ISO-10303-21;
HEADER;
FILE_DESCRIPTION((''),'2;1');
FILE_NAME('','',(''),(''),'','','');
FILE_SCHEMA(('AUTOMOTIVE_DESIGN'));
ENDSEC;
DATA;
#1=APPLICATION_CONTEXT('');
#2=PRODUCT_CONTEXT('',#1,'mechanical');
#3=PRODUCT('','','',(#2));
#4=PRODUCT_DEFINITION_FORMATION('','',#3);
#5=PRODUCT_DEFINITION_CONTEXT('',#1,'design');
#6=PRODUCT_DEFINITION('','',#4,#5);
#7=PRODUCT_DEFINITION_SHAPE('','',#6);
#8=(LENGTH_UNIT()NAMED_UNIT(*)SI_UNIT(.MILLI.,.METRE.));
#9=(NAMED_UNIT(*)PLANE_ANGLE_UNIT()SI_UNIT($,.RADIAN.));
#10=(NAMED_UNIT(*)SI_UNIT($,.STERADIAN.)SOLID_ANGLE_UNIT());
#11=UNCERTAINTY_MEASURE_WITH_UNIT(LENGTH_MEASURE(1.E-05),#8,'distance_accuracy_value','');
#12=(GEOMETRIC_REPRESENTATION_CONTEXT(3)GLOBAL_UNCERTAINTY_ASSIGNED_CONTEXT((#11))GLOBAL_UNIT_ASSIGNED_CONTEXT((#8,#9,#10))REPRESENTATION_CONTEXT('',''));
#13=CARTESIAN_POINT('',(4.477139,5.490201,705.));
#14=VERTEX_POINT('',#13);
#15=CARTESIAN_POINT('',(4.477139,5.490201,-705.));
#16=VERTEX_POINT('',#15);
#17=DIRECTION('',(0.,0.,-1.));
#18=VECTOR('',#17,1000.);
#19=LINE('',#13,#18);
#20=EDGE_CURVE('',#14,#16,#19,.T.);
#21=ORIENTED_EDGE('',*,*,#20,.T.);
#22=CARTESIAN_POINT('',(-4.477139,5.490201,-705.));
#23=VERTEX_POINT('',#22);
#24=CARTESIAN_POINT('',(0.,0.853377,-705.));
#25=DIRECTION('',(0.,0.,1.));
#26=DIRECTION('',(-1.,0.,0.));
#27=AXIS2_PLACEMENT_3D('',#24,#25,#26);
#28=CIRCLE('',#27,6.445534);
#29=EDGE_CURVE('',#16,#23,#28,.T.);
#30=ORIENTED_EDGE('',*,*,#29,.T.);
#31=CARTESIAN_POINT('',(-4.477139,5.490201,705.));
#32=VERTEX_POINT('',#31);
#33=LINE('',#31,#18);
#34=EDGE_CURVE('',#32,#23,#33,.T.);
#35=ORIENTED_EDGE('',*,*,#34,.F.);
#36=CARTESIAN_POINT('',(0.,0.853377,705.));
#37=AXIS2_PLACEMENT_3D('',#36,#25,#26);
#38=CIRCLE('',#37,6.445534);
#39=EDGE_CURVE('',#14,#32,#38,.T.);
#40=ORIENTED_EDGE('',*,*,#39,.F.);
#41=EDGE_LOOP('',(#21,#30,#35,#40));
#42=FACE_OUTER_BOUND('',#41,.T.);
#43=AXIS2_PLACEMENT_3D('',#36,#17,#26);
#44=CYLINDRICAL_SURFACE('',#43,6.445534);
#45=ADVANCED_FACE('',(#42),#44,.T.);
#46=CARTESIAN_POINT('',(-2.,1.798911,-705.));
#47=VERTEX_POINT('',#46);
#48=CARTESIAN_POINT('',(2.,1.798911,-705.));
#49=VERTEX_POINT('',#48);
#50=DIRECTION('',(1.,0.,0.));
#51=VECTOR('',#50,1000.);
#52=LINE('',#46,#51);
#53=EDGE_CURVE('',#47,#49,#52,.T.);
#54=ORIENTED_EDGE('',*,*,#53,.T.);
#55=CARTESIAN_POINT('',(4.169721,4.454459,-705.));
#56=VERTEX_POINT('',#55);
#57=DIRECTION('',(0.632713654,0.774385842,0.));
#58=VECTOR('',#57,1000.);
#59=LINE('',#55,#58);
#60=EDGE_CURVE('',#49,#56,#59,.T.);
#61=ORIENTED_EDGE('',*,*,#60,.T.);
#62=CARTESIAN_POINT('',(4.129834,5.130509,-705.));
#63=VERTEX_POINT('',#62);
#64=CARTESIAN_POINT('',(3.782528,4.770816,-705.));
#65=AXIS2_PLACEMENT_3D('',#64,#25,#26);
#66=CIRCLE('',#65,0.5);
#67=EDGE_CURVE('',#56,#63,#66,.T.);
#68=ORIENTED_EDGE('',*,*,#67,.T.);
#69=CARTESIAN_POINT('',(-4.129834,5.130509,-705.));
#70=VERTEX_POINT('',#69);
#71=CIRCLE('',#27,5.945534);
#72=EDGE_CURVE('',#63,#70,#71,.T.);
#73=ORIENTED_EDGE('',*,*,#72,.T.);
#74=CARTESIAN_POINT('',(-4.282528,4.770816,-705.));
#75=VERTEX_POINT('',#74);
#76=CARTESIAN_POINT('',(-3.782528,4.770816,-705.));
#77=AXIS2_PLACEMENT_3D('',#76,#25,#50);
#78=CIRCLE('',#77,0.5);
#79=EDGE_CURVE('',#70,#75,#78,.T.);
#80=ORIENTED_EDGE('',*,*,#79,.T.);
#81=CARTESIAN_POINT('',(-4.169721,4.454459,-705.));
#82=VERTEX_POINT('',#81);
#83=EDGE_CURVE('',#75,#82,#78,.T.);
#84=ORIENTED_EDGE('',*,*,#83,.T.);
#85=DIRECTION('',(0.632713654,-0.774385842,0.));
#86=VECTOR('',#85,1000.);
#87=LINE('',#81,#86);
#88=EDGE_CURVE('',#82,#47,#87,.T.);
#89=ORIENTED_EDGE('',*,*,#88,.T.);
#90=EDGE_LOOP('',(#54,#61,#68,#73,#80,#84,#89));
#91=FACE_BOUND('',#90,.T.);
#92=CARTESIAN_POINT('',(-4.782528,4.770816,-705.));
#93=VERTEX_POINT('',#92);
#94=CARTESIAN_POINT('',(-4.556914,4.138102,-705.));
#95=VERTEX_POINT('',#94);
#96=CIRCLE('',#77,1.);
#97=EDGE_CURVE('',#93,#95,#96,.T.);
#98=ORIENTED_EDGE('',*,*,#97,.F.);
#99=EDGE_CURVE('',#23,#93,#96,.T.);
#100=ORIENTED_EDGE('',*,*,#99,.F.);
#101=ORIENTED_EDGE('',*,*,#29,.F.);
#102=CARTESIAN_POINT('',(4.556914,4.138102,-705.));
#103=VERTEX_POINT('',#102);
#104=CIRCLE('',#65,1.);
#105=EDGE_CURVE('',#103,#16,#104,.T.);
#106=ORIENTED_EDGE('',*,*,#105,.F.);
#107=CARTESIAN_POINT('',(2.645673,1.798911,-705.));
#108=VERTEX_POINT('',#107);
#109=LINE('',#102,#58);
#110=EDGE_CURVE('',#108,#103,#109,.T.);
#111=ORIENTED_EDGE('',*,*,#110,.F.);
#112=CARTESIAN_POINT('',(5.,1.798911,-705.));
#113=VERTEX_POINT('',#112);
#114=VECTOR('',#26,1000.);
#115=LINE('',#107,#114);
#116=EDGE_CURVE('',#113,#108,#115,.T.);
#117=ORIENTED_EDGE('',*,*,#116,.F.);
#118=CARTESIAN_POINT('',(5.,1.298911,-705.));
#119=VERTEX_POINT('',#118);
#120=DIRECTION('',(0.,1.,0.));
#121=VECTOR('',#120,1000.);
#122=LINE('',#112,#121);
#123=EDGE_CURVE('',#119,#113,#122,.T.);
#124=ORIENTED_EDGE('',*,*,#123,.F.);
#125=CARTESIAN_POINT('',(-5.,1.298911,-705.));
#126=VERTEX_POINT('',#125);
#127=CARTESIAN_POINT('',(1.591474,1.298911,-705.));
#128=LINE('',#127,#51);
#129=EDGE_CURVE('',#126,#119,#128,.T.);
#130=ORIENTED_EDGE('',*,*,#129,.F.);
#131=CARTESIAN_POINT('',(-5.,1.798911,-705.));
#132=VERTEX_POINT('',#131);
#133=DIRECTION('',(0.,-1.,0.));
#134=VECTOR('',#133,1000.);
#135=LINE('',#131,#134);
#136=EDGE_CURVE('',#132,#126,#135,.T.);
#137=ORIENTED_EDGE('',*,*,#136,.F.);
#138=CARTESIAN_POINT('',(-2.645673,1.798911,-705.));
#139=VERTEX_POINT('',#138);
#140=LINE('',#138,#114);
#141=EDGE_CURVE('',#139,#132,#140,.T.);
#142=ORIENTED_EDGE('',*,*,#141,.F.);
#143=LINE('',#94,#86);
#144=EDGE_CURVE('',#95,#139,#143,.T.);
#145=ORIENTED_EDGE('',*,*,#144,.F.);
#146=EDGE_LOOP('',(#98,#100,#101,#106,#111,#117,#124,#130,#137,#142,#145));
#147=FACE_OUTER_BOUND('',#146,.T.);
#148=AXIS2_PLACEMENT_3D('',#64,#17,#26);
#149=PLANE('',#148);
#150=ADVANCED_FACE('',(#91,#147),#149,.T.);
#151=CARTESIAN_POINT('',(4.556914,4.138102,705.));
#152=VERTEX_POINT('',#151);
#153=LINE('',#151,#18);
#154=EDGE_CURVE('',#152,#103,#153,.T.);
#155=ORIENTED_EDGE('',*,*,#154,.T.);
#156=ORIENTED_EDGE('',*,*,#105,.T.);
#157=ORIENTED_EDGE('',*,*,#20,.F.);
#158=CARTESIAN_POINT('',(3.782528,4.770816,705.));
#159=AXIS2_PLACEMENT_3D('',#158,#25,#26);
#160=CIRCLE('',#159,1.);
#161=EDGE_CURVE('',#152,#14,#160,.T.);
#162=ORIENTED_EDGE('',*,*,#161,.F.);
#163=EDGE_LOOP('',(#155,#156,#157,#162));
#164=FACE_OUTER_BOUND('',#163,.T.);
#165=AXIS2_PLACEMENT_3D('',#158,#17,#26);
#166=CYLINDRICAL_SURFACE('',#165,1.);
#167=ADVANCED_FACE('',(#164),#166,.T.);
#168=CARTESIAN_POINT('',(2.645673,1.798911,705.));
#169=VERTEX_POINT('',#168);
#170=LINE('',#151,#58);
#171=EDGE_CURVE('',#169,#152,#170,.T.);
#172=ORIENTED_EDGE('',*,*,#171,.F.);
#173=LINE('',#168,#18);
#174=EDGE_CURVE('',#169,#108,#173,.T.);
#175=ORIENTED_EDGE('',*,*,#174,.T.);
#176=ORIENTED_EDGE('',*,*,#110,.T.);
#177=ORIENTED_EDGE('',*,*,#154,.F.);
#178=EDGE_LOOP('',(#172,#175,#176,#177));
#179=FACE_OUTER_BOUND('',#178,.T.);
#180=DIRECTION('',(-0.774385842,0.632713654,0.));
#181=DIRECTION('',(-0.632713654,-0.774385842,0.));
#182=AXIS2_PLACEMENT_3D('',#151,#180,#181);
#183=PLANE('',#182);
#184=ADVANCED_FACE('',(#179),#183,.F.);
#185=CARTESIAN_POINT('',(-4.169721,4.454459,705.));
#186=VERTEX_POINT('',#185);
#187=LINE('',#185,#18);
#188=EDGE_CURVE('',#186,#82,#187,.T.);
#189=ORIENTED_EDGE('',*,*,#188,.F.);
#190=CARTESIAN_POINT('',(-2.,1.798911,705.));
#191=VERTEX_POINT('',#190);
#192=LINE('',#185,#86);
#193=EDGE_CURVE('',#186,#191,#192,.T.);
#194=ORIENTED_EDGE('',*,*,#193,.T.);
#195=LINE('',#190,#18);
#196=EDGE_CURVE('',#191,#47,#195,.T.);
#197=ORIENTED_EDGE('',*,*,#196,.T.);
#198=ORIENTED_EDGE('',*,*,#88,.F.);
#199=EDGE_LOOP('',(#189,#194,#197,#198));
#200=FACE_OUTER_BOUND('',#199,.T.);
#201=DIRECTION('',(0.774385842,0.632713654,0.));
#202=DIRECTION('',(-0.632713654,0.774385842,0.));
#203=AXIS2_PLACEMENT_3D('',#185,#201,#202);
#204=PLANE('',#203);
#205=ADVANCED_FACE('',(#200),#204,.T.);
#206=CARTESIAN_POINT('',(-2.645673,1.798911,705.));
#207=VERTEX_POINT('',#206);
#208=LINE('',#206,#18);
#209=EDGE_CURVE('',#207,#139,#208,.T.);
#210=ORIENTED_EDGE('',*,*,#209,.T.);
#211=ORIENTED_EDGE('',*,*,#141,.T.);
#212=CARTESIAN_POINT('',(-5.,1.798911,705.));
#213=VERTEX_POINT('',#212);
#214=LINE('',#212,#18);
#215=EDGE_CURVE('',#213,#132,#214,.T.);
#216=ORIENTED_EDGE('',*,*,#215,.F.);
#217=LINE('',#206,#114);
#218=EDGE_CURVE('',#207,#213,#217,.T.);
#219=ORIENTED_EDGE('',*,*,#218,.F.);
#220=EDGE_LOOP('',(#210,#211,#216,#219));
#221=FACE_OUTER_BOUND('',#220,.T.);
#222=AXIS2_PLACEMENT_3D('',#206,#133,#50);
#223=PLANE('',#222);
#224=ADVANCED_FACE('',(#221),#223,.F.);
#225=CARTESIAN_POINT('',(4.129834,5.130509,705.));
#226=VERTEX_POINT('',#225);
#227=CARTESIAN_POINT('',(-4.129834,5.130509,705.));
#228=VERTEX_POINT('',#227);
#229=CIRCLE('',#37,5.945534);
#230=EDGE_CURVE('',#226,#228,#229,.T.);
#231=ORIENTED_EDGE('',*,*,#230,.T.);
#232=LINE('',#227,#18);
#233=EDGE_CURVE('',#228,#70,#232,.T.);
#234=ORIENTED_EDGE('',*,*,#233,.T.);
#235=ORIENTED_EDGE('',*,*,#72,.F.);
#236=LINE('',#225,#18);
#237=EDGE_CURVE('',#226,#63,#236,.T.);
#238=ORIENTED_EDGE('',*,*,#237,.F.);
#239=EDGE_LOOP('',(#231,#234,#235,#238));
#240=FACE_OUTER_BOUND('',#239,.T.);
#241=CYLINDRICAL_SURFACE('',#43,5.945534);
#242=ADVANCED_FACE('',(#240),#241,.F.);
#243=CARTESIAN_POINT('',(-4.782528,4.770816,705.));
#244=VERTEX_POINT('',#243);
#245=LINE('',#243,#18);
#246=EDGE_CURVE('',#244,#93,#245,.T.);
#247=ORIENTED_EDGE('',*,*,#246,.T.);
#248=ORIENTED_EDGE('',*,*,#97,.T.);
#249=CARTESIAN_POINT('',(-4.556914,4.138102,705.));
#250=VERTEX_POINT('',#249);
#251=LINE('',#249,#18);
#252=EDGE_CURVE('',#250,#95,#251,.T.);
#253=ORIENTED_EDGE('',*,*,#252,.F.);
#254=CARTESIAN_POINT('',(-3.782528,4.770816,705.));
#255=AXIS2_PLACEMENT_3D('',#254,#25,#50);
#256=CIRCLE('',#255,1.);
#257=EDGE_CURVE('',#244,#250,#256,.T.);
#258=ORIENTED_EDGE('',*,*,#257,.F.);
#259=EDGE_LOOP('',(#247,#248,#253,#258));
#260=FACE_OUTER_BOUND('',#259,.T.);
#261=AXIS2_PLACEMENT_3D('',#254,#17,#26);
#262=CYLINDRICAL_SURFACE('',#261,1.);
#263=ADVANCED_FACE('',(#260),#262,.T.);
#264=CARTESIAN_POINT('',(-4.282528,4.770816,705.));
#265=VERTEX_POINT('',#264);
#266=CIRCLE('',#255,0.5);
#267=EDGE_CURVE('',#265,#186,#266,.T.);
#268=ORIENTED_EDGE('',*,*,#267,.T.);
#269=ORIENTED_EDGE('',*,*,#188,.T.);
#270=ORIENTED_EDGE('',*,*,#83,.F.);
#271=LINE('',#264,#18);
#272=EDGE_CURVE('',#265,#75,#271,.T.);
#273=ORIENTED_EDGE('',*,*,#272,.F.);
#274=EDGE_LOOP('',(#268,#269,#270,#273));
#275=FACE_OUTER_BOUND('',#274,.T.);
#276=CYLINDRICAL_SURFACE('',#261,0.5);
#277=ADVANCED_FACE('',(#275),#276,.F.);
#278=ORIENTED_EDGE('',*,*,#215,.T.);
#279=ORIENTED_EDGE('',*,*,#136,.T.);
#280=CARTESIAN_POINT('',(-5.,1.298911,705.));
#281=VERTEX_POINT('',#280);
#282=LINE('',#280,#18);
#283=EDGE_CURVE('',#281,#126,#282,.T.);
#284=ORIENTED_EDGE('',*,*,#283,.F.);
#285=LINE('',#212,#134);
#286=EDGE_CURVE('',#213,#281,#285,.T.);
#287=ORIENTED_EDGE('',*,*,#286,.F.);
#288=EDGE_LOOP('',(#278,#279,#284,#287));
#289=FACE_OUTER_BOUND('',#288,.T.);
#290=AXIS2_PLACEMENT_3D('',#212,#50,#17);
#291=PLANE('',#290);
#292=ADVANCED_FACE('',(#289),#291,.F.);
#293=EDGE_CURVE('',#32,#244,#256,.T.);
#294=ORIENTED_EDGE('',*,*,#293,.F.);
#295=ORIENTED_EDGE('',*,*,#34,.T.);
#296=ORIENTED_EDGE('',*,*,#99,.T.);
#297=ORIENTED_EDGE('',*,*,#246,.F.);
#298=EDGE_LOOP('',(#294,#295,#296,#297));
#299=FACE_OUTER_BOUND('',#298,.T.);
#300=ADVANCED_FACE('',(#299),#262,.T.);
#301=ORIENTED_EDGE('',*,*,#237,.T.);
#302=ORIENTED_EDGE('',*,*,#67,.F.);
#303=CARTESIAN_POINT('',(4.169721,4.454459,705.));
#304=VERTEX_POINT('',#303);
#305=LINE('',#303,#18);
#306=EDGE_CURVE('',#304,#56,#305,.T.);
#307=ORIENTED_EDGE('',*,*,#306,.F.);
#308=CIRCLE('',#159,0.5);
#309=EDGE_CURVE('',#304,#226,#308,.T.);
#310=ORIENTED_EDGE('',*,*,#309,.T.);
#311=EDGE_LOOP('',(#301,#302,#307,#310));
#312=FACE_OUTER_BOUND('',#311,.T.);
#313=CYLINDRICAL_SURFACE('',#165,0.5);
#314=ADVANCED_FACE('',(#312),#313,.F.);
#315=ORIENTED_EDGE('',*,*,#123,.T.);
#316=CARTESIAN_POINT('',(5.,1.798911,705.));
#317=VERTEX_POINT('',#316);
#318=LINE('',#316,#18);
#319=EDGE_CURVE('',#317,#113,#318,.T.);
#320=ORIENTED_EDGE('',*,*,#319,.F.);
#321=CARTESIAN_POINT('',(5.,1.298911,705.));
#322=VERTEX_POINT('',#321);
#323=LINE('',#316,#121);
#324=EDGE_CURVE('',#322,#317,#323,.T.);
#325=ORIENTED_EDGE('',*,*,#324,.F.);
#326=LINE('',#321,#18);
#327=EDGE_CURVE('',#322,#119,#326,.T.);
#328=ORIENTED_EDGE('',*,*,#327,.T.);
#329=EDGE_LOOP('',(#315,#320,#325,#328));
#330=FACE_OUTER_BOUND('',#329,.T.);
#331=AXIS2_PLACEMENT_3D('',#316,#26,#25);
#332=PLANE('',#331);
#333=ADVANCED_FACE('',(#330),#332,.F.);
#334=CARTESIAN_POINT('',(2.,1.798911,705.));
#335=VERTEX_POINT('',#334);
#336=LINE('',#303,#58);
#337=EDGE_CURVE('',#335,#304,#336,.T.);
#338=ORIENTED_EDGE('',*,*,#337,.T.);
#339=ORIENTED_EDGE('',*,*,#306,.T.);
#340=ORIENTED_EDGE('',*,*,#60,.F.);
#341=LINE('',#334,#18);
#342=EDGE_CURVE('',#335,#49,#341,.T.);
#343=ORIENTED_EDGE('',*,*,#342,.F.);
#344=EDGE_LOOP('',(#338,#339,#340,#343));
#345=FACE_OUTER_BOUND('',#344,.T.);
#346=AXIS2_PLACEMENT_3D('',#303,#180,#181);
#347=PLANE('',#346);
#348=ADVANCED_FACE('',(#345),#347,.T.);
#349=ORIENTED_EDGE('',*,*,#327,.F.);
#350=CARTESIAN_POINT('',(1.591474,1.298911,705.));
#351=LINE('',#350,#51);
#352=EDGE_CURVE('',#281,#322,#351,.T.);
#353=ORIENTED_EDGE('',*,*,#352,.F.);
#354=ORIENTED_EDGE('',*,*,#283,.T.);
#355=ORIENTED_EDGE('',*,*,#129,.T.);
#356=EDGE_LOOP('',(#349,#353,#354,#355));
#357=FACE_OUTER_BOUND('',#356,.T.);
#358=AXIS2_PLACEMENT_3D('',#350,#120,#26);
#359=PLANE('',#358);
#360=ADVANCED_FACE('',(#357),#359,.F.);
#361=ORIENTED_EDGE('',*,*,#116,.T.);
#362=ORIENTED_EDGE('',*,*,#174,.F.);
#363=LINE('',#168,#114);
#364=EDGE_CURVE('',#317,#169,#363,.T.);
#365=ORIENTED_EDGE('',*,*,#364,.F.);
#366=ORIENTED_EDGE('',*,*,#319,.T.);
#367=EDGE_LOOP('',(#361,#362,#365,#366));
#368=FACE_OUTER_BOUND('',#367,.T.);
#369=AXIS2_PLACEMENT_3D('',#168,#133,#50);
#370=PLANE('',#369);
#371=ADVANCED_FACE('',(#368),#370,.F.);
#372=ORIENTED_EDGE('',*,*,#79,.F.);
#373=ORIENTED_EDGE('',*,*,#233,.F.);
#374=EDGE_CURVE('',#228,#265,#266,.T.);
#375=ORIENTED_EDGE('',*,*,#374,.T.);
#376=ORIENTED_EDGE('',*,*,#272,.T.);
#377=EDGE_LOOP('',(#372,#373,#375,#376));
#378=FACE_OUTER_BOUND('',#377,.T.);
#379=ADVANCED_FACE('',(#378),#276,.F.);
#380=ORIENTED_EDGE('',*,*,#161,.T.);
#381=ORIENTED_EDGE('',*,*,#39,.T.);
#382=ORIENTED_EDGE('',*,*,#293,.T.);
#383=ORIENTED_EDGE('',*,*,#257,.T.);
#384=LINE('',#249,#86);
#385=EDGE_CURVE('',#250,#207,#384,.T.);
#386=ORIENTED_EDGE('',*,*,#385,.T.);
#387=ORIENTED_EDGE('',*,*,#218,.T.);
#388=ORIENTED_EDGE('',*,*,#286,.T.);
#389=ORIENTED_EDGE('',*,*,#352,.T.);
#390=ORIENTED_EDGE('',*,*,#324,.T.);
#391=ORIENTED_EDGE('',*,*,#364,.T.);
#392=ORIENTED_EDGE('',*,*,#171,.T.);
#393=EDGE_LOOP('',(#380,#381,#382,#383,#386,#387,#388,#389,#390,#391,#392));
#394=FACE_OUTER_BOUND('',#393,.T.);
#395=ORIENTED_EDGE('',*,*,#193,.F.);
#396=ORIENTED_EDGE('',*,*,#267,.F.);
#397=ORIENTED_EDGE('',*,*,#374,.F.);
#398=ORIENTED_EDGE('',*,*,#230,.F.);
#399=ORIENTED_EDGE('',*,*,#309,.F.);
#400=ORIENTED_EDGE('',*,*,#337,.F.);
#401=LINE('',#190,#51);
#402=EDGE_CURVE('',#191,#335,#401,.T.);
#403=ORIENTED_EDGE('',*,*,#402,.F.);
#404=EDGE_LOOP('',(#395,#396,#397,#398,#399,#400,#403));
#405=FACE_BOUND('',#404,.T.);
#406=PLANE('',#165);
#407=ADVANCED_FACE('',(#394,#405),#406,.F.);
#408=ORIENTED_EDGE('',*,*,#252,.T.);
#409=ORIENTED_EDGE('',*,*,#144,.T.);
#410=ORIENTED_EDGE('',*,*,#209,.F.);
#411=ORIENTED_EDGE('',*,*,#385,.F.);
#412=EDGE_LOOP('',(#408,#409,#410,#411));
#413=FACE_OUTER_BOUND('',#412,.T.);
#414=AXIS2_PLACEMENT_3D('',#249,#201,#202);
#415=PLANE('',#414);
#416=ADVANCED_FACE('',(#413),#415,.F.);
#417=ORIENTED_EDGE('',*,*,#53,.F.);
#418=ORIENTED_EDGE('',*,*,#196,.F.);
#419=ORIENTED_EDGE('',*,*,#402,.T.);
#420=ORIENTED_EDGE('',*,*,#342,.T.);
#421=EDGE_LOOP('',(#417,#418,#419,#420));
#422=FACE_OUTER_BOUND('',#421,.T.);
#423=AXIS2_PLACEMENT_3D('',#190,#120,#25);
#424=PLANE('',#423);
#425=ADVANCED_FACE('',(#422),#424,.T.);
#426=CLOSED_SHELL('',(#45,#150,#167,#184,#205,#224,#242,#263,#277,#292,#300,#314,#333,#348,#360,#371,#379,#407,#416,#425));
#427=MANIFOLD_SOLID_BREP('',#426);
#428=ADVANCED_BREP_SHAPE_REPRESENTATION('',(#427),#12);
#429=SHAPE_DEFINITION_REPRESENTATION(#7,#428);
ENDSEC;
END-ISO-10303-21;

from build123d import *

# Parameters (mm, degrees)
EXTRUDE_1_DEPTH = 705


with BuildPart() as part:
    # 草图1 → 凸台-拉伸1 (new, symmetric)
    with BuildSketch(Plane.XY):
        with BuildLine():
            Line((-4.556913863, 4.138102128), (-2.645672962, 1.79891143))
            Line((-2.645672962, 1.79891143), (-5, 1.79891143))
            Line((-5, 1.79891143), (-5, 1.29891143))
            Line((-5, 1.29891143), (1.591473901, 1.29891143))
            Line((1.591473901, 1.29891143), (5, 1.29891143))
            Line((5, 1.29891143), (5, 1.79891143))
            Line((5, 1.79891143), (2.645672962, 1.79891143))
            Line((2.645672962, 1.79891143), (4.556913863, 4.138102128))
            ThreePointArc((4.556913863, 4.138102128), (4.780792009, 4.829714088), (4.47713902, 5.490201325))
            ThreePointArc((4.47713902, 5.490201325), (0, 7.29891143), (-4.47713902, 5.490201325))
            ThreePointArc((-4.47713902, 5.490201325), (-4.780792009, 4.829714088), (-4.556913863, 4.138102128))
        make_face()
        with BuildLine():
            Line((-2, 1.79891143), (2, 1.79891143))
            Line((2, 1.79891143), (4.169720942, 4.454458955))
            ThreePointArc((4.169720942, 4.454458955), (4.281660015, 4.800264935), (4.12983352, 5.130508554))
            ThreePointArc((4.12983352, 5.130508554), (0, 6.79891143), (-4.12983352, 5.130508554))
            ThreePointArc((-4.12983352, 5.130508554), (-4.281660015, 4.800264935), (-4.169720942, 4.454458955))
            Line((-4.169720942, 4.454458955), (-2, 1.79891143))
        make_face(mode=Mode.SUBTRACT)
    extrude(amount=EXTRUDE_1_DEPTH, both=True)


solid = part.part
